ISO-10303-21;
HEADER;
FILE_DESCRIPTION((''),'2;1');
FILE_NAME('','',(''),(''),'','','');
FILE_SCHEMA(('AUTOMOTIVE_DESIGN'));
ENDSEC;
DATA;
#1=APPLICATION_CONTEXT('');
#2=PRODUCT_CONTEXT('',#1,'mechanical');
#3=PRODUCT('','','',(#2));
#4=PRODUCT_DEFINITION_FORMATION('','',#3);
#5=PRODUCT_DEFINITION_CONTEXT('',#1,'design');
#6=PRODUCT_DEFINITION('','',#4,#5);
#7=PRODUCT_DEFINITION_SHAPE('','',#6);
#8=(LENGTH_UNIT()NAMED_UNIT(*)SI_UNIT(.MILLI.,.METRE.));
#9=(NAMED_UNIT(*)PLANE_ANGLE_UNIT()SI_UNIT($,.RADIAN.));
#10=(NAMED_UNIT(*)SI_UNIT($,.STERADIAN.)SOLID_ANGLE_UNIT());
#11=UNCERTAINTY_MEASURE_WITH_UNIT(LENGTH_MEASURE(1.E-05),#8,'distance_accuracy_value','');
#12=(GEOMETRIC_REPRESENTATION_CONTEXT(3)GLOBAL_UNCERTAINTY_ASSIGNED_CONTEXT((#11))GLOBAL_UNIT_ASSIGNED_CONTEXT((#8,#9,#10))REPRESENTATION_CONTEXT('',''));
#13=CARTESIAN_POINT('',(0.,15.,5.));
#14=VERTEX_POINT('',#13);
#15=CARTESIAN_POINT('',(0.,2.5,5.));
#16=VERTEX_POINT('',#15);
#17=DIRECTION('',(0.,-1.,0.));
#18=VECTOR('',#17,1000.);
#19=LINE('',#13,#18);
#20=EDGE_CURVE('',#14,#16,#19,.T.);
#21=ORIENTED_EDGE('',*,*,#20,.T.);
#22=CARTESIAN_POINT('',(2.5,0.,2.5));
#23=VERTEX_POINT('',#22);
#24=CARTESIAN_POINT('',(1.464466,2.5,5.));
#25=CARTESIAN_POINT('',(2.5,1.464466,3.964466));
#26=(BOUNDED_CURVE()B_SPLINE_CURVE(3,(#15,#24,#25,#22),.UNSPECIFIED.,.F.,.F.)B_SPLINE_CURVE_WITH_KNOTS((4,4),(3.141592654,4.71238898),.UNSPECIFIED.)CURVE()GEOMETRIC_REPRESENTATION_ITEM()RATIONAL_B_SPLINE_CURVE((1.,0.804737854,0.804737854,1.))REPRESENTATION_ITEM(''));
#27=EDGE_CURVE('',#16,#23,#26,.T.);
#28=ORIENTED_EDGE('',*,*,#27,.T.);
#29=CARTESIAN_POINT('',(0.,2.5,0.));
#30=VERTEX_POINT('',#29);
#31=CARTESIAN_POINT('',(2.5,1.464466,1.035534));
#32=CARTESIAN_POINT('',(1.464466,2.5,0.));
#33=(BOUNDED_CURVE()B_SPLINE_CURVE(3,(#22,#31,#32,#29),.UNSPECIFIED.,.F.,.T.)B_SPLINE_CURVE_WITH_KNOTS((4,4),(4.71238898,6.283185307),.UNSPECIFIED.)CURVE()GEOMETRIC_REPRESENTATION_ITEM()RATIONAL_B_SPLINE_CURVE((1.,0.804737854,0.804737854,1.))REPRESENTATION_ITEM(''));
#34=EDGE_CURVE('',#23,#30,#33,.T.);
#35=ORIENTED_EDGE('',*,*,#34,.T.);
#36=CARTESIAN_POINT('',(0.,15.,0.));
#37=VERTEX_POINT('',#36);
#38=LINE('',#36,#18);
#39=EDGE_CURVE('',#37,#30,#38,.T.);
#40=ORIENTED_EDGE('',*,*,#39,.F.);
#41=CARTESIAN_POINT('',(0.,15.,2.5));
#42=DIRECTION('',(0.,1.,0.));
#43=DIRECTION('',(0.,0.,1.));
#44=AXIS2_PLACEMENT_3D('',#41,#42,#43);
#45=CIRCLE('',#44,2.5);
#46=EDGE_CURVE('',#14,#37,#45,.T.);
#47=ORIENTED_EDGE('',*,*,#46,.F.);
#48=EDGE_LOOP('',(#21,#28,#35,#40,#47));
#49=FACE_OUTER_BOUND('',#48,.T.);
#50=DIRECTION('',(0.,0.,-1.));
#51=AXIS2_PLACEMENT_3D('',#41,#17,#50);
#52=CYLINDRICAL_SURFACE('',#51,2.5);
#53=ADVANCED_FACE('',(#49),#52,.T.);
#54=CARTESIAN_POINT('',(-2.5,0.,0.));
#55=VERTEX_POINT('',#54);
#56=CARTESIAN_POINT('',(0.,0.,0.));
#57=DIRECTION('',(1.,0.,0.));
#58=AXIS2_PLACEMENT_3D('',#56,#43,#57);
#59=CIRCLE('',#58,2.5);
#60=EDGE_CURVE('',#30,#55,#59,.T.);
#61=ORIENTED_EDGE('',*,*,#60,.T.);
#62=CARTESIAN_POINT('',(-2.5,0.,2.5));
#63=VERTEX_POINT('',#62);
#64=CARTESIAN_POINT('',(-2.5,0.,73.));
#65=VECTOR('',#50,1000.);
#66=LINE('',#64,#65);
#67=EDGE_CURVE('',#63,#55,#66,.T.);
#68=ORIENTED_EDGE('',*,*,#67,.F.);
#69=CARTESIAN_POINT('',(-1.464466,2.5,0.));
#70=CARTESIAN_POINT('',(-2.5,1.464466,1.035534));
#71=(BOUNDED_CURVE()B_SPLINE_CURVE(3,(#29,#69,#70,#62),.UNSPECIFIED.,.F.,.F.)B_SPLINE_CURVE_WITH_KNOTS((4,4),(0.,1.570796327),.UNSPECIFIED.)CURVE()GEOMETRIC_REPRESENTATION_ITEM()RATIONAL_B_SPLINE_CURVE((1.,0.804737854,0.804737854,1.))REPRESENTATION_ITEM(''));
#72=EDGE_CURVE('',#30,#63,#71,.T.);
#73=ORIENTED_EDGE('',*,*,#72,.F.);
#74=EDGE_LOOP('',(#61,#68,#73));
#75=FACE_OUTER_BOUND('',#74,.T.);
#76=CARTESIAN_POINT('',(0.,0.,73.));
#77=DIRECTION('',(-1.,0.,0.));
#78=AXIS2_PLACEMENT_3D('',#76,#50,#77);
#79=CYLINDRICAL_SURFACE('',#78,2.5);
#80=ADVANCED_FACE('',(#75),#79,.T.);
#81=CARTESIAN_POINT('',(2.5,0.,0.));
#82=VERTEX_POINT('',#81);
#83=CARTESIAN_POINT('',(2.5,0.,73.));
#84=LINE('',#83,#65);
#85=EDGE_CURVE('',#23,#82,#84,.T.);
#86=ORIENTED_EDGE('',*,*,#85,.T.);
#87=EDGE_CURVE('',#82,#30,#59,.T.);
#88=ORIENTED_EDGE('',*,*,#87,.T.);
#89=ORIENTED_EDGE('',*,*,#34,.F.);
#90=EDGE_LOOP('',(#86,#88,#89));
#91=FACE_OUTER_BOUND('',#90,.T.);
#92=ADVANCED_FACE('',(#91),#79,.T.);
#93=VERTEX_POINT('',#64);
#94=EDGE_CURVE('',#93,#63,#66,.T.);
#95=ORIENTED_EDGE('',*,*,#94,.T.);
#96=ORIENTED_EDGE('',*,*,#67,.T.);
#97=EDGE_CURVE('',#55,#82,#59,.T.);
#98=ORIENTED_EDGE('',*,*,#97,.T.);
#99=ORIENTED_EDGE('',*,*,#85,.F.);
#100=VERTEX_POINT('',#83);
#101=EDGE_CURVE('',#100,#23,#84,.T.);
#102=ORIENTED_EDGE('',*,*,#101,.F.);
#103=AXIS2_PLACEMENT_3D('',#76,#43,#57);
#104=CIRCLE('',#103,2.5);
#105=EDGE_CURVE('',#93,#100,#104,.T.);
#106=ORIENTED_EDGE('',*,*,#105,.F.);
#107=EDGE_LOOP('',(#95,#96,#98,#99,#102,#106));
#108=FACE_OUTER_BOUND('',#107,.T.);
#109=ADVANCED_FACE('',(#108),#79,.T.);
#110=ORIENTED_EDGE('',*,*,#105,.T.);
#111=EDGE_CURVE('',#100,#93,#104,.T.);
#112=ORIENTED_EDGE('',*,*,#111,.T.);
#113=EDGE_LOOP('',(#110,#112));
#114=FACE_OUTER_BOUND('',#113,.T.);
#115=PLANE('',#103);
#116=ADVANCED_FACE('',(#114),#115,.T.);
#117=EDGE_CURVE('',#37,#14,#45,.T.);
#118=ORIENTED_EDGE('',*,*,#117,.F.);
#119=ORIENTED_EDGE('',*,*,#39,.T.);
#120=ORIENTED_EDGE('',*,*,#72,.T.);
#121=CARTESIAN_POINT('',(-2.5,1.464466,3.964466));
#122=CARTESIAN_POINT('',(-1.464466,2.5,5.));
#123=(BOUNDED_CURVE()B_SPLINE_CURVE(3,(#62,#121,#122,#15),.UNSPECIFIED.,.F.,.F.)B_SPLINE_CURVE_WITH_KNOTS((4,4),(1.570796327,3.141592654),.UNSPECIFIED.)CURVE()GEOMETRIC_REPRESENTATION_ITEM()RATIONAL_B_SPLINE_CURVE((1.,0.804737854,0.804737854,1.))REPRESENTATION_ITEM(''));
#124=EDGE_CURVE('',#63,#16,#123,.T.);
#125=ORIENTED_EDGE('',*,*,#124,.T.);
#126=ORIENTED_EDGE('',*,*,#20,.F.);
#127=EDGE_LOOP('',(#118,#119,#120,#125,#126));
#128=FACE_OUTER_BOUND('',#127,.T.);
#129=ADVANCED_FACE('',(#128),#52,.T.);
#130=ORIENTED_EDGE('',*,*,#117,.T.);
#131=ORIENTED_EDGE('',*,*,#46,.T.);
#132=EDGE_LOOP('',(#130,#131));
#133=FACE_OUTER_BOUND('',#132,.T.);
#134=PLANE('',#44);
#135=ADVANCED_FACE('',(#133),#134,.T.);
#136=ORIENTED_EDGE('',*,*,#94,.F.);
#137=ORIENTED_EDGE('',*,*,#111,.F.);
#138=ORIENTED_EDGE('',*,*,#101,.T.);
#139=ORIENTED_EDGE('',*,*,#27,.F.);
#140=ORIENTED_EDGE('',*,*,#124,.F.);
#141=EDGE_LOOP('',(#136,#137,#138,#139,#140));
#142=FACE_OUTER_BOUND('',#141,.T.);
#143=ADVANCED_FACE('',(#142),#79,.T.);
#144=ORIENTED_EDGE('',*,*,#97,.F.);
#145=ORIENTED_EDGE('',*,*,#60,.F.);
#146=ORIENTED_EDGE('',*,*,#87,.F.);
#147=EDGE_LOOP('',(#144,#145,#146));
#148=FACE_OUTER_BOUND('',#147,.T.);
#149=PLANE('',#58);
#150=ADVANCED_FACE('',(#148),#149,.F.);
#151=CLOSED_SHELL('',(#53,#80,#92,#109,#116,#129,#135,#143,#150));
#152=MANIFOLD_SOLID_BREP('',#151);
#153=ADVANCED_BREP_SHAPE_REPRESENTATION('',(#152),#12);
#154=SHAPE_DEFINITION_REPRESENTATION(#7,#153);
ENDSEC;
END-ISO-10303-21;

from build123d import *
from build123d.topology import SkipClean

# Parameters (mm, degrees)
SKETCH_1_R      = 2.5
EXTRUDE_1_DEPTH = 73
SKETCH_2_R      = 2.5
EXTRUDE_2_DEPTH = 15


with BuildPart() as part:
    # 草图1 → 凸台-拉伸1 (new body)
    with BuildSketch(Plane.XY):
        Circle(SKETCH_1_R)
    extrude(amount=EXTRUDE_1_DEPTH)

    # 草图2 → 凸台-拉伸2 (add)
    with SkipClean():  # the faces are left unmerged after this step: merging them gives an invalid solid
        with BuildSketch(Plane(origin=(0, 0, 0), x_dir=(1, 0, 0), z_dir=(0, 1, 0))):
            with Locations(Location((0, -2.5, 0), (0, 0, 90))):
                Circle(SKETCH_2_R)
        extrude(amount=EXTRUDE_2_DEPTH)


solid = part.part
